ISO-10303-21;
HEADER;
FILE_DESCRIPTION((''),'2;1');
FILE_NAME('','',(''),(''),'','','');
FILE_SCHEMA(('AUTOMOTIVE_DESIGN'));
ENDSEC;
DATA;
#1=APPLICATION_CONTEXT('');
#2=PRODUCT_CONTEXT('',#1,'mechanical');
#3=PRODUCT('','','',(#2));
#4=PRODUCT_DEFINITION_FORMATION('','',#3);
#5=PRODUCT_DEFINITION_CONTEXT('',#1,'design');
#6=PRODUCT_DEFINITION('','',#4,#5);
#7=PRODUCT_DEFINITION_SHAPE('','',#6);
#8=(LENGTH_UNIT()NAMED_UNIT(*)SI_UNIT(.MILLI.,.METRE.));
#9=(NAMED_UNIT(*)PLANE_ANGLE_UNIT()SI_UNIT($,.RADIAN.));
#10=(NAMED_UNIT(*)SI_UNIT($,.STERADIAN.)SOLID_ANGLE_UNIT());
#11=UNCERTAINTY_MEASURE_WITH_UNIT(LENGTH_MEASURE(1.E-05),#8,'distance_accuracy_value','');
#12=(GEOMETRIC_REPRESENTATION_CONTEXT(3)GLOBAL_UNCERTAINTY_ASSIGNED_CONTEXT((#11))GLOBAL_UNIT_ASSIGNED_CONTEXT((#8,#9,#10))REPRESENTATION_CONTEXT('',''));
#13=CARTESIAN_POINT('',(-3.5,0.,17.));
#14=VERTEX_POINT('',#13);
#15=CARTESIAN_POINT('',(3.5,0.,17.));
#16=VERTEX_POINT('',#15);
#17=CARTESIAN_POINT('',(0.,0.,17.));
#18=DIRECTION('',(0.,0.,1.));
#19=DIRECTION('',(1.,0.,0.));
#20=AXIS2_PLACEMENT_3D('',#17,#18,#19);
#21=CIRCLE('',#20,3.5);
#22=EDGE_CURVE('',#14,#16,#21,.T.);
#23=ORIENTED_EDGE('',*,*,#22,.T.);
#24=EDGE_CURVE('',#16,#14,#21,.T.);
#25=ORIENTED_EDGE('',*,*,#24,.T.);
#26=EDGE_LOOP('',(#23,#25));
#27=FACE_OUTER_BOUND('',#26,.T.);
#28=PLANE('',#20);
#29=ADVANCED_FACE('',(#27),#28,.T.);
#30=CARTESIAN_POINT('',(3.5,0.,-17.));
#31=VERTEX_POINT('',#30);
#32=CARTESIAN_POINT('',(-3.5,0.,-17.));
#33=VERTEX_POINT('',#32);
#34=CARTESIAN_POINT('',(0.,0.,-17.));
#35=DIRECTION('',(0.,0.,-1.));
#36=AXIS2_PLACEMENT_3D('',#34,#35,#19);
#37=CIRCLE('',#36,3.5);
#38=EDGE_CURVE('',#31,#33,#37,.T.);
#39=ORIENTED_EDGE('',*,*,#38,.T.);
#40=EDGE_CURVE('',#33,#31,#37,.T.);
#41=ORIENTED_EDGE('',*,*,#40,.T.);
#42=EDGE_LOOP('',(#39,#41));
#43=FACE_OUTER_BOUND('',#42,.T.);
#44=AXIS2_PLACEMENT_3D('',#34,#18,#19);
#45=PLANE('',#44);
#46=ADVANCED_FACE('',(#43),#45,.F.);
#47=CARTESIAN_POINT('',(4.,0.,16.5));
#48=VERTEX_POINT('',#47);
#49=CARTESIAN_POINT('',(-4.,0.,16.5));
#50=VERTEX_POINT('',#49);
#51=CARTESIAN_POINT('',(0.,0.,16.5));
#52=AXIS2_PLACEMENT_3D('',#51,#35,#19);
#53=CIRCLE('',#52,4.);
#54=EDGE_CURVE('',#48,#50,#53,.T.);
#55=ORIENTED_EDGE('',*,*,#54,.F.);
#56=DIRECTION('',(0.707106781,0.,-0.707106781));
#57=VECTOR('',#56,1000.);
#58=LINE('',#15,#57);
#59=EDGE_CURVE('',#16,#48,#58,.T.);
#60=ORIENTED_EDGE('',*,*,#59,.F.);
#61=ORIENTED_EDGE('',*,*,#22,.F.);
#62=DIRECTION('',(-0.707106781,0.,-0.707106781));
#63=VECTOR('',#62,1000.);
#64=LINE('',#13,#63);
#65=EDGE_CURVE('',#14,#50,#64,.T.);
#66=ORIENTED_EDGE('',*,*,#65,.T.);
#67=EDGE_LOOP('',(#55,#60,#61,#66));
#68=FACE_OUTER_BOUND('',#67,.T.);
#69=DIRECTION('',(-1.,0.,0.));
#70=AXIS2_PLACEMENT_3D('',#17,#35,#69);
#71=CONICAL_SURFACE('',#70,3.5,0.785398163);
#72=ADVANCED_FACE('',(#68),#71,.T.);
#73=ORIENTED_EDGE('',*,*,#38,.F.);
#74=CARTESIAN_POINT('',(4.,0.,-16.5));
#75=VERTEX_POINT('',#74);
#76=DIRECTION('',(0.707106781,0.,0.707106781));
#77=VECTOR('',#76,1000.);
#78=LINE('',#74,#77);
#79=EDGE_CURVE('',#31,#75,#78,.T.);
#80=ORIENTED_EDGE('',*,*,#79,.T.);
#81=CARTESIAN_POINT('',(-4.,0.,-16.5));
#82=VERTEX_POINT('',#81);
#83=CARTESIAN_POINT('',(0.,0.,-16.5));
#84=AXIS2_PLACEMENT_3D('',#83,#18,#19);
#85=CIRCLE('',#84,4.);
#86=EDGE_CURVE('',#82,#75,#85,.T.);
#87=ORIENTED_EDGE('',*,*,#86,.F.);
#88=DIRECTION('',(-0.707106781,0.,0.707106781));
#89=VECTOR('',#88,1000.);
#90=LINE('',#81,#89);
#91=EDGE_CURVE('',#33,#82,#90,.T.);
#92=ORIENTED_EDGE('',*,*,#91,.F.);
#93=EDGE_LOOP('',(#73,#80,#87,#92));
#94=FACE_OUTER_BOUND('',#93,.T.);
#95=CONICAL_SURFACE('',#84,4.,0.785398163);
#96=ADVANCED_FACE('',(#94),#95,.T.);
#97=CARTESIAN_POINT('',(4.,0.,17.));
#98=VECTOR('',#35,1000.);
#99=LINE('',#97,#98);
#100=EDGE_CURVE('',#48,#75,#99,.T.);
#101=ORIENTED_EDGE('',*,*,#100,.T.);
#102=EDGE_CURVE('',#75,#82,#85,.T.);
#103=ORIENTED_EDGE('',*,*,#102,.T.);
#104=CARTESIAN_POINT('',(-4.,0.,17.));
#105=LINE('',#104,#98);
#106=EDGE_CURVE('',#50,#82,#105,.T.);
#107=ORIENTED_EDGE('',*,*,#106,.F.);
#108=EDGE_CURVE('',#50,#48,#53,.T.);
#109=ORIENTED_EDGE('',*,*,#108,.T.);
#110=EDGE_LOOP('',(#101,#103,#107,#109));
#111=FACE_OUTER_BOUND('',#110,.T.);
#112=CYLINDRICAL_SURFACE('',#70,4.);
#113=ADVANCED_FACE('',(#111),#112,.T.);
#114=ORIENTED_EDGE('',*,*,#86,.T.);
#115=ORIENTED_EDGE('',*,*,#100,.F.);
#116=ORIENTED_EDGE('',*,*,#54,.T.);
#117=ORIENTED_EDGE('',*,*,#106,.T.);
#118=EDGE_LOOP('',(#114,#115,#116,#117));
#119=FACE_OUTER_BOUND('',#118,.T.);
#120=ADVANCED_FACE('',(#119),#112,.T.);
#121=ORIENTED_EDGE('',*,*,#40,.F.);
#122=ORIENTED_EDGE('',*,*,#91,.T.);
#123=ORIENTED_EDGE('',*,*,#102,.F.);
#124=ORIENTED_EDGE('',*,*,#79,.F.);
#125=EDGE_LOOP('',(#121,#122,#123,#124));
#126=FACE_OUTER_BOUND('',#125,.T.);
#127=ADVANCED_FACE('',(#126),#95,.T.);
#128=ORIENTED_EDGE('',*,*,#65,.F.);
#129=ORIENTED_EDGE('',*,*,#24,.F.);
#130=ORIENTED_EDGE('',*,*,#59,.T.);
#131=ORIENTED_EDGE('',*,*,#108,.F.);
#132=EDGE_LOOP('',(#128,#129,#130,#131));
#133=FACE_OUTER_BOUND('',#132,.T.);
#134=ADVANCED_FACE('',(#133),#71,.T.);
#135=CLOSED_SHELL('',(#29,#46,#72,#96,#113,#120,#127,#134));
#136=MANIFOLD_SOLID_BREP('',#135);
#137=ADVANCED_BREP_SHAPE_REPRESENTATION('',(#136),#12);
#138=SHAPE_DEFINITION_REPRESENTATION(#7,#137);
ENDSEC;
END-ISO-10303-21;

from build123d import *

# Parameters (mm, degrees)
SKETCH1_R           = 4
BOSS_EXTRUDE1_DEPTH = 17
CHAMFER1_SIZE       = 0.5


with BuildPart() as part:
    # Sketch1 → Boss-Extrude1 (new, symmetric)
    with BuildSketch(Plane.XY):
        Circle(SKETCH1_R)
    extrude(amount=BOSS_EXTRUDE1_DEPTH, both=True)

    # Chamfer1
    chamfer1_edges = [part.edges().sort_by_distance(p)[0] for p in [
        (-4, 0, -17),
        (-4, 0, 17),
    ]]
    chamfer(chamfer1_edges, length=CHAMFER1_SIZE)


solid = part.part
